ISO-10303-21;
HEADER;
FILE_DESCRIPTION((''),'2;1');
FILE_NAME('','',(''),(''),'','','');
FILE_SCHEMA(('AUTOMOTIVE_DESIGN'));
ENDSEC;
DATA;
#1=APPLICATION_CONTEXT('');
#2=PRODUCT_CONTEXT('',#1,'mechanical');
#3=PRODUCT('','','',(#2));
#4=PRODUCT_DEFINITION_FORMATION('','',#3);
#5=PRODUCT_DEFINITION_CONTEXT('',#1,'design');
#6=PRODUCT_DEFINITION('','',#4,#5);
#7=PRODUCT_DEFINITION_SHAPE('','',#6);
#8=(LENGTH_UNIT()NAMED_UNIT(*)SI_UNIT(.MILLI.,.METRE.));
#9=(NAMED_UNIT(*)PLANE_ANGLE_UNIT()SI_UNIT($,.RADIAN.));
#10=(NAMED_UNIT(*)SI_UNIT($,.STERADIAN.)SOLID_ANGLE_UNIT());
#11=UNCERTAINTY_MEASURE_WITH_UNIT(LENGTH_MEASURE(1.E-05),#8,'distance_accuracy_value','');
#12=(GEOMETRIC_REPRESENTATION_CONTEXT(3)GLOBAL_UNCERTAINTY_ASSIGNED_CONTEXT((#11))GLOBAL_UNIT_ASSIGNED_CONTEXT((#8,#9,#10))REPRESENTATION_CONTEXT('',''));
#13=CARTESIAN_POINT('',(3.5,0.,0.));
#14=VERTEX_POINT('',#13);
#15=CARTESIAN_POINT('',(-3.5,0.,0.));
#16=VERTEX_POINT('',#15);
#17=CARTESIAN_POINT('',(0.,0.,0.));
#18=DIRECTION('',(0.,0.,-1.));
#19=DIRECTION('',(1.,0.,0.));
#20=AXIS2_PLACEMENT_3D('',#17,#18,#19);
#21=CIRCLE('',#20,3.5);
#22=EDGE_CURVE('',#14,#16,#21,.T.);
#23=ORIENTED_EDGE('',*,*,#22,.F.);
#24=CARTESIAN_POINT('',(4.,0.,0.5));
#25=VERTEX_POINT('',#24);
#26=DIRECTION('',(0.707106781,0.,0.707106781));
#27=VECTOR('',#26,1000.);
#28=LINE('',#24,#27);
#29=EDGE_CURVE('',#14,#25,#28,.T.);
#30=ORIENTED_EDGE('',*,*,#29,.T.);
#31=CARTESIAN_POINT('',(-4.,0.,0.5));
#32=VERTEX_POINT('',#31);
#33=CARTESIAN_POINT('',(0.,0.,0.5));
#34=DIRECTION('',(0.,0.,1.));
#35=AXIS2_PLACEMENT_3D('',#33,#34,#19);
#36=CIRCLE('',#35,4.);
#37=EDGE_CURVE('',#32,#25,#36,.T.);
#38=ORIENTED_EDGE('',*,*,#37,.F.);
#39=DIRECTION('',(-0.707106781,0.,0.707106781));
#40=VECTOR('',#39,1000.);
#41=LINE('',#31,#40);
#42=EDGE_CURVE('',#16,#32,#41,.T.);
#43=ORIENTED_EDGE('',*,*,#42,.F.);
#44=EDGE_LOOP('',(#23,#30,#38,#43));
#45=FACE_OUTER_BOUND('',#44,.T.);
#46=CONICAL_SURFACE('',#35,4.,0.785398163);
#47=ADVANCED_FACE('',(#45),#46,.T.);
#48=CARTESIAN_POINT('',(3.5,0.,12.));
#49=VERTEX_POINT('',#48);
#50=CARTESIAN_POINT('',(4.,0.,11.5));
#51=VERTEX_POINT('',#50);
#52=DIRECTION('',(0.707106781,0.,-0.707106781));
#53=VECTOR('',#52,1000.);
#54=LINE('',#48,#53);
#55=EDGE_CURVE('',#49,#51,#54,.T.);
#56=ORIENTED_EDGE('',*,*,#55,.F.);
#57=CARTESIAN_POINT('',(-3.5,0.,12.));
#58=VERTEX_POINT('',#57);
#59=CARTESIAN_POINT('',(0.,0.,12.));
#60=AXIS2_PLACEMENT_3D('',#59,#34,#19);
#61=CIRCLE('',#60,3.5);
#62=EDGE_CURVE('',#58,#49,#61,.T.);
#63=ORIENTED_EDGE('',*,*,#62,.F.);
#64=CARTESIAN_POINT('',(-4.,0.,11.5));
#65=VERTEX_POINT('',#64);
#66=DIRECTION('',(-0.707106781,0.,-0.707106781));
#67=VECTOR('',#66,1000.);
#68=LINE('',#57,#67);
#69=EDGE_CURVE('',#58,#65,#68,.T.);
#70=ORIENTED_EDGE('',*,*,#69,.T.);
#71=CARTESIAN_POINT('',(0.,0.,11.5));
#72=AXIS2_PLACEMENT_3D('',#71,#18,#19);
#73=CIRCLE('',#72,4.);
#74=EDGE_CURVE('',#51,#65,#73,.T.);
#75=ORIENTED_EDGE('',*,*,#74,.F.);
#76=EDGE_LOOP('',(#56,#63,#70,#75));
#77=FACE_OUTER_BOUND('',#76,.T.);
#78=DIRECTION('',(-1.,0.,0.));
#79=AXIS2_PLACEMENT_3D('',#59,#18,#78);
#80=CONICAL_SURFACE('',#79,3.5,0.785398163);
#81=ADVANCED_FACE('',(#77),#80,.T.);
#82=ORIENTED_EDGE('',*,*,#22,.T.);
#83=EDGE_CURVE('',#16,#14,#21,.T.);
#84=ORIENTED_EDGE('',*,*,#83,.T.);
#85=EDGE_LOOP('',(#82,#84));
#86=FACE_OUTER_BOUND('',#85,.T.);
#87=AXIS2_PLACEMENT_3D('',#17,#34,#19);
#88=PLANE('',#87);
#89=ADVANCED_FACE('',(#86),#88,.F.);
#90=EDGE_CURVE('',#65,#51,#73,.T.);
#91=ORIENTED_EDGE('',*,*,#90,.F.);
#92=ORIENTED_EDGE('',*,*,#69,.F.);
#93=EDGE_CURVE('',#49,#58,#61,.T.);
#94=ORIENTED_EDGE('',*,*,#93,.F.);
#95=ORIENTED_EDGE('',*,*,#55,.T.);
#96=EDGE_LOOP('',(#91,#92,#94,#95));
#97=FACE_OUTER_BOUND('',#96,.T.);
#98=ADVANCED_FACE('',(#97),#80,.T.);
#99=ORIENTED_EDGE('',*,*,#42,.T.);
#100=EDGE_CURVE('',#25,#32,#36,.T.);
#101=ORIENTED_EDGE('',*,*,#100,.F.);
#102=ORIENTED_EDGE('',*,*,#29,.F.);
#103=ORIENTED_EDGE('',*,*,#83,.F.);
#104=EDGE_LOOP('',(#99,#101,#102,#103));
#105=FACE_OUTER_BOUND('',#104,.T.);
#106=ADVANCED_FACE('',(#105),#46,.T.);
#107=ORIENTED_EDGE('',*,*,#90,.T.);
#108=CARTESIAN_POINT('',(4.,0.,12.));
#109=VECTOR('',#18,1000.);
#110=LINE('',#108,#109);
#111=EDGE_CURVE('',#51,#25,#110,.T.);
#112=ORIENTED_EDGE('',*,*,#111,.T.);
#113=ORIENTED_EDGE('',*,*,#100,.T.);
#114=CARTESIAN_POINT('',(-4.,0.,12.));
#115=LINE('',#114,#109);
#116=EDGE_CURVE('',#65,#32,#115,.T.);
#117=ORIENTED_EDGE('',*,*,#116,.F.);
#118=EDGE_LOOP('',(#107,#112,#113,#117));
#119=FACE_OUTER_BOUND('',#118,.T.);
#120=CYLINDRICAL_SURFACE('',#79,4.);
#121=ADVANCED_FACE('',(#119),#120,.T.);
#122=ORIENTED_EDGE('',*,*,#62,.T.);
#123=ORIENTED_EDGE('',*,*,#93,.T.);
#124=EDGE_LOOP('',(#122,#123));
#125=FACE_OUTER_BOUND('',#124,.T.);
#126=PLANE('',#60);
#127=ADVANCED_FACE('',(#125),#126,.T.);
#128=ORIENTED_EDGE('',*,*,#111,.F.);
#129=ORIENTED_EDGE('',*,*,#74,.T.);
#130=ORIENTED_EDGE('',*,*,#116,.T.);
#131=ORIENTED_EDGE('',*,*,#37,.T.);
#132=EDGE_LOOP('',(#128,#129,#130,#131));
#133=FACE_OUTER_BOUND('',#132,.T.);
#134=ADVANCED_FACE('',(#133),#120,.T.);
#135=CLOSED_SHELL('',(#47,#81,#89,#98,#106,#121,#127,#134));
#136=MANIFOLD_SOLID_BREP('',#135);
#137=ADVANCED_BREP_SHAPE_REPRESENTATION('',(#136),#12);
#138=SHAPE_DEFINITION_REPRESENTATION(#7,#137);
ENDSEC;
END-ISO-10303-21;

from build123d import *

# Parameters (mm, degrees)
SKETCH1_R           = 4
BOSS_EXTRUDE1_DEPTH = 12
CHAMFER1_SIZE       = 0.5


with BuildPart() as part:
    # Sketch1 → Boss-Extrude1 (new body)
    with BuildSketch(Plane.XY):
        Circle(SKETCH1_R)
    extrude(amount=BOSS_EXTRUDE1_DEPTH)

    # Chamfer1
    chamfer1_edges = [part.edges().sort_by_distance(p)[0] for p in [
        (-4, 0, 0),
        (-4, 0, 12),
    ]]
    chamfer(chamfer1_edges, length=CHAMFER1_SIZE)


solid = part.part
